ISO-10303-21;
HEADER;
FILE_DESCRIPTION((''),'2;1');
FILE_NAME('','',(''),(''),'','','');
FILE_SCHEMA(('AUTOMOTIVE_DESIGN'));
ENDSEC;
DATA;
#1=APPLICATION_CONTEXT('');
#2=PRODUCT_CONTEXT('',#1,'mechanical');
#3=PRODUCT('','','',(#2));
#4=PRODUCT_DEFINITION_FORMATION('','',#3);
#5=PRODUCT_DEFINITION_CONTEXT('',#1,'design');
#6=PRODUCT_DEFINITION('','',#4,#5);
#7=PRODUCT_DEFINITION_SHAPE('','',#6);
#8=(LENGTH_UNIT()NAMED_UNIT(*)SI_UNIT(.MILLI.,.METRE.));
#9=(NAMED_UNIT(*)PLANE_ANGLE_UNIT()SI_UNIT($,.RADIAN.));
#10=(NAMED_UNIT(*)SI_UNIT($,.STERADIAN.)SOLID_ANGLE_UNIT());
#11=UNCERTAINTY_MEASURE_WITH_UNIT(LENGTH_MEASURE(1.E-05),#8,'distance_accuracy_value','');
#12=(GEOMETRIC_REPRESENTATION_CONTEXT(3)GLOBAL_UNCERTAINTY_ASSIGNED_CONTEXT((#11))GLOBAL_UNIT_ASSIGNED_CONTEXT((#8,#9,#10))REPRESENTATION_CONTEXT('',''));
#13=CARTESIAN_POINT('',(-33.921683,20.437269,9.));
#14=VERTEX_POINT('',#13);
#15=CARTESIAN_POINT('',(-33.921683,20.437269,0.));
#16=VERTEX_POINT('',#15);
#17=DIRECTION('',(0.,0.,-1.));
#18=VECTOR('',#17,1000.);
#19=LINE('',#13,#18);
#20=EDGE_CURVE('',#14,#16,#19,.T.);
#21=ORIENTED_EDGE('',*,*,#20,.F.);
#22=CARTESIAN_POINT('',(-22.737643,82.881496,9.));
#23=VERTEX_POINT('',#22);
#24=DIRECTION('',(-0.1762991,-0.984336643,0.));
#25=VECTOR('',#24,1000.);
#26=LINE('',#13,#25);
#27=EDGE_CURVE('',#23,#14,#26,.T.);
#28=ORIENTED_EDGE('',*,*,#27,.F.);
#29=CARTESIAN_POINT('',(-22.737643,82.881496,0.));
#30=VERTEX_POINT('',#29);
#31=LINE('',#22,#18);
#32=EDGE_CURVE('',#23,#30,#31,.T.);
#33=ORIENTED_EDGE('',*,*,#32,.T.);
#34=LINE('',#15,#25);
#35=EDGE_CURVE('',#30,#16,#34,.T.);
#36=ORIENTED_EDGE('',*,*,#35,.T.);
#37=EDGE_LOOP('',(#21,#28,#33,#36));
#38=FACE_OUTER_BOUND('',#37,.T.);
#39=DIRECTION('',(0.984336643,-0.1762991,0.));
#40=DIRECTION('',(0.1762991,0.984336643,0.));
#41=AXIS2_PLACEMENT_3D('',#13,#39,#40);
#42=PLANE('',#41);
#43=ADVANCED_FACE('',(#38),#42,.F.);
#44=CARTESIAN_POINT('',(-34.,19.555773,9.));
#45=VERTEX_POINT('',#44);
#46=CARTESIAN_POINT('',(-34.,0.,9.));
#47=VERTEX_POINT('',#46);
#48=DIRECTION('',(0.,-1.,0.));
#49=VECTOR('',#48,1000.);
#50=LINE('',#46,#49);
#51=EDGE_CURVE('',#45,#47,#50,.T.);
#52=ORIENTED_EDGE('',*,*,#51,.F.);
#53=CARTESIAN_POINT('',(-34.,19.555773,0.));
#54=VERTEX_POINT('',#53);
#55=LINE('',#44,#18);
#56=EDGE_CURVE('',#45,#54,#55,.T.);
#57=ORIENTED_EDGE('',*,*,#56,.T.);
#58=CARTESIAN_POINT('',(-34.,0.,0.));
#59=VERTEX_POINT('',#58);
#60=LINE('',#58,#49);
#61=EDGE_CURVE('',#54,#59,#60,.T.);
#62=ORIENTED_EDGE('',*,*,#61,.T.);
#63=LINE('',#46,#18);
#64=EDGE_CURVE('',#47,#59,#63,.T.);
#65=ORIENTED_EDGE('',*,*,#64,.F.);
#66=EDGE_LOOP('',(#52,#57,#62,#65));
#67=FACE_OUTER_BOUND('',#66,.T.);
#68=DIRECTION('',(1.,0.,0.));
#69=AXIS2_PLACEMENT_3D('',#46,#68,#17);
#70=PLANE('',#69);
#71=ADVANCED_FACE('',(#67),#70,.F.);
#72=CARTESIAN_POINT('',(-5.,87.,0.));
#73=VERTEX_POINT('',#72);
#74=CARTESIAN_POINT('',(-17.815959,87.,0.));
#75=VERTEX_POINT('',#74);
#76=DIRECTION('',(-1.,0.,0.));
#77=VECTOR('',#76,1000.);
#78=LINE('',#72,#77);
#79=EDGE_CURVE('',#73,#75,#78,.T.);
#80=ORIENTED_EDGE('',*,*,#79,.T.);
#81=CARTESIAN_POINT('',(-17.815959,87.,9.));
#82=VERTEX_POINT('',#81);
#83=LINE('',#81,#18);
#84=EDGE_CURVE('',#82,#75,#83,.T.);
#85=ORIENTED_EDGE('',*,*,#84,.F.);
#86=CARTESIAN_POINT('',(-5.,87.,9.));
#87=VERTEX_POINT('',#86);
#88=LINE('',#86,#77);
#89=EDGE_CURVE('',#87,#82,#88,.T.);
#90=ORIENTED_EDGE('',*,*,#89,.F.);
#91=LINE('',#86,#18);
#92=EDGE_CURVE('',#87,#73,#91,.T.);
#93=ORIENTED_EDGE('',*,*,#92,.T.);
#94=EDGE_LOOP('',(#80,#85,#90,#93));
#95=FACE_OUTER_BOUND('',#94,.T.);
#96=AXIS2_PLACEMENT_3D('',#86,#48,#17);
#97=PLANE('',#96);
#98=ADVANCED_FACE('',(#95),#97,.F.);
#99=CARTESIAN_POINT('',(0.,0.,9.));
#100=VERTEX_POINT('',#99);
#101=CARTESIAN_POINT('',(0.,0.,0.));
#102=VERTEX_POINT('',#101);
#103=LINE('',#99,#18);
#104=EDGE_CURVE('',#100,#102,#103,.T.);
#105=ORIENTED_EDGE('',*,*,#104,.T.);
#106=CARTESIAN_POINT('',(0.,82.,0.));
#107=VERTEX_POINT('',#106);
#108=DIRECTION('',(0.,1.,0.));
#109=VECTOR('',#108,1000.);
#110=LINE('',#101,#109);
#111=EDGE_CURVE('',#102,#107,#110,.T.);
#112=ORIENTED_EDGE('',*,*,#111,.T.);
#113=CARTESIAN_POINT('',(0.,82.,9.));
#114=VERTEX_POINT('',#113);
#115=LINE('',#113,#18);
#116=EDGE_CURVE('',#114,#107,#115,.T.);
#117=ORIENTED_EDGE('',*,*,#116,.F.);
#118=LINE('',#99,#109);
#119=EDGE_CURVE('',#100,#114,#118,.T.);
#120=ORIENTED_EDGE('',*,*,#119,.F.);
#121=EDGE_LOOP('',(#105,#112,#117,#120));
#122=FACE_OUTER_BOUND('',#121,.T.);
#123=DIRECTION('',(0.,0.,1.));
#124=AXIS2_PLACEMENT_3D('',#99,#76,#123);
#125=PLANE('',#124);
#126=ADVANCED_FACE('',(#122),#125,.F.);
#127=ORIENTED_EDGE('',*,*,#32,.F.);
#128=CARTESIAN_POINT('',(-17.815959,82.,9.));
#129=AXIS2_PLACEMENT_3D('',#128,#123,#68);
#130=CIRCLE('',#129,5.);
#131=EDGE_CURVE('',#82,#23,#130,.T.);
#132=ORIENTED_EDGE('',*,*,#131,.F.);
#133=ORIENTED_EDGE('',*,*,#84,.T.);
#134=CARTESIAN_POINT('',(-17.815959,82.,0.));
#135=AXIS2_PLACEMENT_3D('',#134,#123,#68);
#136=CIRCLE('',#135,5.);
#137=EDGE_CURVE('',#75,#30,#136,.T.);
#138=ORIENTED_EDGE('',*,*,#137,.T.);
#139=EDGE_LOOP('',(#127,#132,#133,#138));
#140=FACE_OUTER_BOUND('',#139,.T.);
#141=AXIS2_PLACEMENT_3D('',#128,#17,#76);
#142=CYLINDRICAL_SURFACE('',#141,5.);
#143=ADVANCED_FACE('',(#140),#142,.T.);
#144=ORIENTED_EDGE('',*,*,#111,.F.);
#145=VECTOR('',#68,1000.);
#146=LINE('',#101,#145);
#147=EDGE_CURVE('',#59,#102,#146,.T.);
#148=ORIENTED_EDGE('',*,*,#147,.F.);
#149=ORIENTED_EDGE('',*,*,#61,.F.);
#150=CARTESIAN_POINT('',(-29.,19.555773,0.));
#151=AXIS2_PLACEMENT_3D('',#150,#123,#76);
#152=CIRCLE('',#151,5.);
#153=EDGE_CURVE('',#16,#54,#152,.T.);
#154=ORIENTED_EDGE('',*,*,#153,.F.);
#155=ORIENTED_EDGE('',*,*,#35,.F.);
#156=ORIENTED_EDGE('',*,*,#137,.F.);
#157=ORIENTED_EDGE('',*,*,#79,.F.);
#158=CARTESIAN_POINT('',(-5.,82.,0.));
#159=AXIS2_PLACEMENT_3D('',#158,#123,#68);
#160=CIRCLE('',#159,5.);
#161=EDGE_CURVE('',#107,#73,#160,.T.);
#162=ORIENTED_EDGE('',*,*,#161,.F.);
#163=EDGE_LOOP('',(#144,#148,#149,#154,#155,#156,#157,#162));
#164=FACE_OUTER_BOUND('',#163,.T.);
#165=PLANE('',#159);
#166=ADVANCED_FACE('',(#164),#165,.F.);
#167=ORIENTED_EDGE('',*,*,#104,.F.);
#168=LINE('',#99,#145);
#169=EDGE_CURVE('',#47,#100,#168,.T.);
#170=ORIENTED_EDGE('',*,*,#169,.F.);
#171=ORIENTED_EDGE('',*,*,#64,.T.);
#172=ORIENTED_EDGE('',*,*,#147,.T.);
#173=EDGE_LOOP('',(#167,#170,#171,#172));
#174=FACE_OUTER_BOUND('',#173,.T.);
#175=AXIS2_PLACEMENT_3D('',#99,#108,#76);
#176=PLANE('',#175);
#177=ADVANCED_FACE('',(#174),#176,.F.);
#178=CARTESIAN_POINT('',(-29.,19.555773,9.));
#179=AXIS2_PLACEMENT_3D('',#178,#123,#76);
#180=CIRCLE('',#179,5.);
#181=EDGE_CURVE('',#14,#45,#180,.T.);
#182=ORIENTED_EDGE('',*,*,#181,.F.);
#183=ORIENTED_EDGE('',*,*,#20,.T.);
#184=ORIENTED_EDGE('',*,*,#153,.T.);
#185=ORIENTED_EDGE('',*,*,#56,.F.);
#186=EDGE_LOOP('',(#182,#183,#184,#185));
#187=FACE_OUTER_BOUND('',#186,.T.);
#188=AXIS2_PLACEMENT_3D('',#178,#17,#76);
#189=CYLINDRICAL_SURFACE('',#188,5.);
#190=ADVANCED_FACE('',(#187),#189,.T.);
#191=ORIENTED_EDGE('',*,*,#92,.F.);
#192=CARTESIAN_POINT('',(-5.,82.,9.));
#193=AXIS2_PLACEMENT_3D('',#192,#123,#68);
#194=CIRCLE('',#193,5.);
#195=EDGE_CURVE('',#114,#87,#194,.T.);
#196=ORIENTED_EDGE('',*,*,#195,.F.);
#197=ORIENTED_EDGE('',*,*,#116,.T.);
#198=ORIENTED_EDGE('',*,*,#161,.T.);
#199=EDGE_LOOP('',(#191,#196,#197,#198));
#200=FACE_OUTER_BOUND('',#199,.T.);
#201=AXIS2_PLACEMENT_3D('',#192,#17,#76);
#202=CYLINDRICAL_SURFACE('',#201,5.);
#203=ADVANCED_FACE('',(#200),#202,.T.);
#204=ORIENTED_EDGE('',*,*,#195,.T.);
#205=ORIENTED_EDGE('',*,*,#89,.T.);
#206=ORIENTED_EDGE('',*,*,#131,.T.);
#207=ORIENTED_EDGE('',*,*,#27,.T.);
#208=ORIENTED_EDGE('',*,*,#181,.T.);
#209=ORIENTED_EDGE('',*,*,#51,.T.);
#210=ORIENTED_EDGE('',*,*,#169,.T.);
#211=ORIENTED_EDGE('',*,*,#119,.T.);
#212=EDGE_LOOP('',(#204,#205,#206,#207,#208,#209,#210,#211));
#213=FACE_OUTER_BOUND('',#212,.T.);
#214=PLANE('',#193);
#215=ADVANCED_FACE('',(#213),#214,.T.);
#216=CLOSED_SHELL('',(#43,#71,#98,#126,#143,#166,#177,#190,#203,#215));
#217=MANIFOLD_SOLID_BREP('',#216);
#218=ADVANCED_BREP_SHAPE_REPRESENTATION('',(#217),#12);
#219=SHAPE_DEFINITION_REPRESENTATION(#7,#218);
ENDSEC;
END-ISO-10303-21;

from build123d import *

# Parameters (mm, degrees)
BOSS_EXTRUDE1_DEPTH = 9


with BuildPart() as part:
    # Sketch1 → Boss-Extrude1 (new body)
    with BuildSketch(Plane.XY):
        with BuildLine():
            Line((0, 0), (-34, 0))
            Line((-34, 0), (-34, 19.555773208))
            ThreePointArc((-34, 19.555773208), (-33.980382319, 19.99825706), (-33.921683216, 20.437268709))
            Line((-33.921683216, 20.437268709), (-22.737642597, 82.881495501))
            ThreePointArc((-22.737642597, 82.881495501), (-21.024738159, 85.834545443), (-17.815959381, 87))
            Line((-17.815959381, 87), (-5, 87))
            ThreePointArc((-5, 87), (-1.464466094, 85.535533906), (0, 82))
            Line((0, 82), (0, 0))
        make_face()
    extrude(amount=BOSS_EXTRUDE1_DEPTH)


solid = part.part
